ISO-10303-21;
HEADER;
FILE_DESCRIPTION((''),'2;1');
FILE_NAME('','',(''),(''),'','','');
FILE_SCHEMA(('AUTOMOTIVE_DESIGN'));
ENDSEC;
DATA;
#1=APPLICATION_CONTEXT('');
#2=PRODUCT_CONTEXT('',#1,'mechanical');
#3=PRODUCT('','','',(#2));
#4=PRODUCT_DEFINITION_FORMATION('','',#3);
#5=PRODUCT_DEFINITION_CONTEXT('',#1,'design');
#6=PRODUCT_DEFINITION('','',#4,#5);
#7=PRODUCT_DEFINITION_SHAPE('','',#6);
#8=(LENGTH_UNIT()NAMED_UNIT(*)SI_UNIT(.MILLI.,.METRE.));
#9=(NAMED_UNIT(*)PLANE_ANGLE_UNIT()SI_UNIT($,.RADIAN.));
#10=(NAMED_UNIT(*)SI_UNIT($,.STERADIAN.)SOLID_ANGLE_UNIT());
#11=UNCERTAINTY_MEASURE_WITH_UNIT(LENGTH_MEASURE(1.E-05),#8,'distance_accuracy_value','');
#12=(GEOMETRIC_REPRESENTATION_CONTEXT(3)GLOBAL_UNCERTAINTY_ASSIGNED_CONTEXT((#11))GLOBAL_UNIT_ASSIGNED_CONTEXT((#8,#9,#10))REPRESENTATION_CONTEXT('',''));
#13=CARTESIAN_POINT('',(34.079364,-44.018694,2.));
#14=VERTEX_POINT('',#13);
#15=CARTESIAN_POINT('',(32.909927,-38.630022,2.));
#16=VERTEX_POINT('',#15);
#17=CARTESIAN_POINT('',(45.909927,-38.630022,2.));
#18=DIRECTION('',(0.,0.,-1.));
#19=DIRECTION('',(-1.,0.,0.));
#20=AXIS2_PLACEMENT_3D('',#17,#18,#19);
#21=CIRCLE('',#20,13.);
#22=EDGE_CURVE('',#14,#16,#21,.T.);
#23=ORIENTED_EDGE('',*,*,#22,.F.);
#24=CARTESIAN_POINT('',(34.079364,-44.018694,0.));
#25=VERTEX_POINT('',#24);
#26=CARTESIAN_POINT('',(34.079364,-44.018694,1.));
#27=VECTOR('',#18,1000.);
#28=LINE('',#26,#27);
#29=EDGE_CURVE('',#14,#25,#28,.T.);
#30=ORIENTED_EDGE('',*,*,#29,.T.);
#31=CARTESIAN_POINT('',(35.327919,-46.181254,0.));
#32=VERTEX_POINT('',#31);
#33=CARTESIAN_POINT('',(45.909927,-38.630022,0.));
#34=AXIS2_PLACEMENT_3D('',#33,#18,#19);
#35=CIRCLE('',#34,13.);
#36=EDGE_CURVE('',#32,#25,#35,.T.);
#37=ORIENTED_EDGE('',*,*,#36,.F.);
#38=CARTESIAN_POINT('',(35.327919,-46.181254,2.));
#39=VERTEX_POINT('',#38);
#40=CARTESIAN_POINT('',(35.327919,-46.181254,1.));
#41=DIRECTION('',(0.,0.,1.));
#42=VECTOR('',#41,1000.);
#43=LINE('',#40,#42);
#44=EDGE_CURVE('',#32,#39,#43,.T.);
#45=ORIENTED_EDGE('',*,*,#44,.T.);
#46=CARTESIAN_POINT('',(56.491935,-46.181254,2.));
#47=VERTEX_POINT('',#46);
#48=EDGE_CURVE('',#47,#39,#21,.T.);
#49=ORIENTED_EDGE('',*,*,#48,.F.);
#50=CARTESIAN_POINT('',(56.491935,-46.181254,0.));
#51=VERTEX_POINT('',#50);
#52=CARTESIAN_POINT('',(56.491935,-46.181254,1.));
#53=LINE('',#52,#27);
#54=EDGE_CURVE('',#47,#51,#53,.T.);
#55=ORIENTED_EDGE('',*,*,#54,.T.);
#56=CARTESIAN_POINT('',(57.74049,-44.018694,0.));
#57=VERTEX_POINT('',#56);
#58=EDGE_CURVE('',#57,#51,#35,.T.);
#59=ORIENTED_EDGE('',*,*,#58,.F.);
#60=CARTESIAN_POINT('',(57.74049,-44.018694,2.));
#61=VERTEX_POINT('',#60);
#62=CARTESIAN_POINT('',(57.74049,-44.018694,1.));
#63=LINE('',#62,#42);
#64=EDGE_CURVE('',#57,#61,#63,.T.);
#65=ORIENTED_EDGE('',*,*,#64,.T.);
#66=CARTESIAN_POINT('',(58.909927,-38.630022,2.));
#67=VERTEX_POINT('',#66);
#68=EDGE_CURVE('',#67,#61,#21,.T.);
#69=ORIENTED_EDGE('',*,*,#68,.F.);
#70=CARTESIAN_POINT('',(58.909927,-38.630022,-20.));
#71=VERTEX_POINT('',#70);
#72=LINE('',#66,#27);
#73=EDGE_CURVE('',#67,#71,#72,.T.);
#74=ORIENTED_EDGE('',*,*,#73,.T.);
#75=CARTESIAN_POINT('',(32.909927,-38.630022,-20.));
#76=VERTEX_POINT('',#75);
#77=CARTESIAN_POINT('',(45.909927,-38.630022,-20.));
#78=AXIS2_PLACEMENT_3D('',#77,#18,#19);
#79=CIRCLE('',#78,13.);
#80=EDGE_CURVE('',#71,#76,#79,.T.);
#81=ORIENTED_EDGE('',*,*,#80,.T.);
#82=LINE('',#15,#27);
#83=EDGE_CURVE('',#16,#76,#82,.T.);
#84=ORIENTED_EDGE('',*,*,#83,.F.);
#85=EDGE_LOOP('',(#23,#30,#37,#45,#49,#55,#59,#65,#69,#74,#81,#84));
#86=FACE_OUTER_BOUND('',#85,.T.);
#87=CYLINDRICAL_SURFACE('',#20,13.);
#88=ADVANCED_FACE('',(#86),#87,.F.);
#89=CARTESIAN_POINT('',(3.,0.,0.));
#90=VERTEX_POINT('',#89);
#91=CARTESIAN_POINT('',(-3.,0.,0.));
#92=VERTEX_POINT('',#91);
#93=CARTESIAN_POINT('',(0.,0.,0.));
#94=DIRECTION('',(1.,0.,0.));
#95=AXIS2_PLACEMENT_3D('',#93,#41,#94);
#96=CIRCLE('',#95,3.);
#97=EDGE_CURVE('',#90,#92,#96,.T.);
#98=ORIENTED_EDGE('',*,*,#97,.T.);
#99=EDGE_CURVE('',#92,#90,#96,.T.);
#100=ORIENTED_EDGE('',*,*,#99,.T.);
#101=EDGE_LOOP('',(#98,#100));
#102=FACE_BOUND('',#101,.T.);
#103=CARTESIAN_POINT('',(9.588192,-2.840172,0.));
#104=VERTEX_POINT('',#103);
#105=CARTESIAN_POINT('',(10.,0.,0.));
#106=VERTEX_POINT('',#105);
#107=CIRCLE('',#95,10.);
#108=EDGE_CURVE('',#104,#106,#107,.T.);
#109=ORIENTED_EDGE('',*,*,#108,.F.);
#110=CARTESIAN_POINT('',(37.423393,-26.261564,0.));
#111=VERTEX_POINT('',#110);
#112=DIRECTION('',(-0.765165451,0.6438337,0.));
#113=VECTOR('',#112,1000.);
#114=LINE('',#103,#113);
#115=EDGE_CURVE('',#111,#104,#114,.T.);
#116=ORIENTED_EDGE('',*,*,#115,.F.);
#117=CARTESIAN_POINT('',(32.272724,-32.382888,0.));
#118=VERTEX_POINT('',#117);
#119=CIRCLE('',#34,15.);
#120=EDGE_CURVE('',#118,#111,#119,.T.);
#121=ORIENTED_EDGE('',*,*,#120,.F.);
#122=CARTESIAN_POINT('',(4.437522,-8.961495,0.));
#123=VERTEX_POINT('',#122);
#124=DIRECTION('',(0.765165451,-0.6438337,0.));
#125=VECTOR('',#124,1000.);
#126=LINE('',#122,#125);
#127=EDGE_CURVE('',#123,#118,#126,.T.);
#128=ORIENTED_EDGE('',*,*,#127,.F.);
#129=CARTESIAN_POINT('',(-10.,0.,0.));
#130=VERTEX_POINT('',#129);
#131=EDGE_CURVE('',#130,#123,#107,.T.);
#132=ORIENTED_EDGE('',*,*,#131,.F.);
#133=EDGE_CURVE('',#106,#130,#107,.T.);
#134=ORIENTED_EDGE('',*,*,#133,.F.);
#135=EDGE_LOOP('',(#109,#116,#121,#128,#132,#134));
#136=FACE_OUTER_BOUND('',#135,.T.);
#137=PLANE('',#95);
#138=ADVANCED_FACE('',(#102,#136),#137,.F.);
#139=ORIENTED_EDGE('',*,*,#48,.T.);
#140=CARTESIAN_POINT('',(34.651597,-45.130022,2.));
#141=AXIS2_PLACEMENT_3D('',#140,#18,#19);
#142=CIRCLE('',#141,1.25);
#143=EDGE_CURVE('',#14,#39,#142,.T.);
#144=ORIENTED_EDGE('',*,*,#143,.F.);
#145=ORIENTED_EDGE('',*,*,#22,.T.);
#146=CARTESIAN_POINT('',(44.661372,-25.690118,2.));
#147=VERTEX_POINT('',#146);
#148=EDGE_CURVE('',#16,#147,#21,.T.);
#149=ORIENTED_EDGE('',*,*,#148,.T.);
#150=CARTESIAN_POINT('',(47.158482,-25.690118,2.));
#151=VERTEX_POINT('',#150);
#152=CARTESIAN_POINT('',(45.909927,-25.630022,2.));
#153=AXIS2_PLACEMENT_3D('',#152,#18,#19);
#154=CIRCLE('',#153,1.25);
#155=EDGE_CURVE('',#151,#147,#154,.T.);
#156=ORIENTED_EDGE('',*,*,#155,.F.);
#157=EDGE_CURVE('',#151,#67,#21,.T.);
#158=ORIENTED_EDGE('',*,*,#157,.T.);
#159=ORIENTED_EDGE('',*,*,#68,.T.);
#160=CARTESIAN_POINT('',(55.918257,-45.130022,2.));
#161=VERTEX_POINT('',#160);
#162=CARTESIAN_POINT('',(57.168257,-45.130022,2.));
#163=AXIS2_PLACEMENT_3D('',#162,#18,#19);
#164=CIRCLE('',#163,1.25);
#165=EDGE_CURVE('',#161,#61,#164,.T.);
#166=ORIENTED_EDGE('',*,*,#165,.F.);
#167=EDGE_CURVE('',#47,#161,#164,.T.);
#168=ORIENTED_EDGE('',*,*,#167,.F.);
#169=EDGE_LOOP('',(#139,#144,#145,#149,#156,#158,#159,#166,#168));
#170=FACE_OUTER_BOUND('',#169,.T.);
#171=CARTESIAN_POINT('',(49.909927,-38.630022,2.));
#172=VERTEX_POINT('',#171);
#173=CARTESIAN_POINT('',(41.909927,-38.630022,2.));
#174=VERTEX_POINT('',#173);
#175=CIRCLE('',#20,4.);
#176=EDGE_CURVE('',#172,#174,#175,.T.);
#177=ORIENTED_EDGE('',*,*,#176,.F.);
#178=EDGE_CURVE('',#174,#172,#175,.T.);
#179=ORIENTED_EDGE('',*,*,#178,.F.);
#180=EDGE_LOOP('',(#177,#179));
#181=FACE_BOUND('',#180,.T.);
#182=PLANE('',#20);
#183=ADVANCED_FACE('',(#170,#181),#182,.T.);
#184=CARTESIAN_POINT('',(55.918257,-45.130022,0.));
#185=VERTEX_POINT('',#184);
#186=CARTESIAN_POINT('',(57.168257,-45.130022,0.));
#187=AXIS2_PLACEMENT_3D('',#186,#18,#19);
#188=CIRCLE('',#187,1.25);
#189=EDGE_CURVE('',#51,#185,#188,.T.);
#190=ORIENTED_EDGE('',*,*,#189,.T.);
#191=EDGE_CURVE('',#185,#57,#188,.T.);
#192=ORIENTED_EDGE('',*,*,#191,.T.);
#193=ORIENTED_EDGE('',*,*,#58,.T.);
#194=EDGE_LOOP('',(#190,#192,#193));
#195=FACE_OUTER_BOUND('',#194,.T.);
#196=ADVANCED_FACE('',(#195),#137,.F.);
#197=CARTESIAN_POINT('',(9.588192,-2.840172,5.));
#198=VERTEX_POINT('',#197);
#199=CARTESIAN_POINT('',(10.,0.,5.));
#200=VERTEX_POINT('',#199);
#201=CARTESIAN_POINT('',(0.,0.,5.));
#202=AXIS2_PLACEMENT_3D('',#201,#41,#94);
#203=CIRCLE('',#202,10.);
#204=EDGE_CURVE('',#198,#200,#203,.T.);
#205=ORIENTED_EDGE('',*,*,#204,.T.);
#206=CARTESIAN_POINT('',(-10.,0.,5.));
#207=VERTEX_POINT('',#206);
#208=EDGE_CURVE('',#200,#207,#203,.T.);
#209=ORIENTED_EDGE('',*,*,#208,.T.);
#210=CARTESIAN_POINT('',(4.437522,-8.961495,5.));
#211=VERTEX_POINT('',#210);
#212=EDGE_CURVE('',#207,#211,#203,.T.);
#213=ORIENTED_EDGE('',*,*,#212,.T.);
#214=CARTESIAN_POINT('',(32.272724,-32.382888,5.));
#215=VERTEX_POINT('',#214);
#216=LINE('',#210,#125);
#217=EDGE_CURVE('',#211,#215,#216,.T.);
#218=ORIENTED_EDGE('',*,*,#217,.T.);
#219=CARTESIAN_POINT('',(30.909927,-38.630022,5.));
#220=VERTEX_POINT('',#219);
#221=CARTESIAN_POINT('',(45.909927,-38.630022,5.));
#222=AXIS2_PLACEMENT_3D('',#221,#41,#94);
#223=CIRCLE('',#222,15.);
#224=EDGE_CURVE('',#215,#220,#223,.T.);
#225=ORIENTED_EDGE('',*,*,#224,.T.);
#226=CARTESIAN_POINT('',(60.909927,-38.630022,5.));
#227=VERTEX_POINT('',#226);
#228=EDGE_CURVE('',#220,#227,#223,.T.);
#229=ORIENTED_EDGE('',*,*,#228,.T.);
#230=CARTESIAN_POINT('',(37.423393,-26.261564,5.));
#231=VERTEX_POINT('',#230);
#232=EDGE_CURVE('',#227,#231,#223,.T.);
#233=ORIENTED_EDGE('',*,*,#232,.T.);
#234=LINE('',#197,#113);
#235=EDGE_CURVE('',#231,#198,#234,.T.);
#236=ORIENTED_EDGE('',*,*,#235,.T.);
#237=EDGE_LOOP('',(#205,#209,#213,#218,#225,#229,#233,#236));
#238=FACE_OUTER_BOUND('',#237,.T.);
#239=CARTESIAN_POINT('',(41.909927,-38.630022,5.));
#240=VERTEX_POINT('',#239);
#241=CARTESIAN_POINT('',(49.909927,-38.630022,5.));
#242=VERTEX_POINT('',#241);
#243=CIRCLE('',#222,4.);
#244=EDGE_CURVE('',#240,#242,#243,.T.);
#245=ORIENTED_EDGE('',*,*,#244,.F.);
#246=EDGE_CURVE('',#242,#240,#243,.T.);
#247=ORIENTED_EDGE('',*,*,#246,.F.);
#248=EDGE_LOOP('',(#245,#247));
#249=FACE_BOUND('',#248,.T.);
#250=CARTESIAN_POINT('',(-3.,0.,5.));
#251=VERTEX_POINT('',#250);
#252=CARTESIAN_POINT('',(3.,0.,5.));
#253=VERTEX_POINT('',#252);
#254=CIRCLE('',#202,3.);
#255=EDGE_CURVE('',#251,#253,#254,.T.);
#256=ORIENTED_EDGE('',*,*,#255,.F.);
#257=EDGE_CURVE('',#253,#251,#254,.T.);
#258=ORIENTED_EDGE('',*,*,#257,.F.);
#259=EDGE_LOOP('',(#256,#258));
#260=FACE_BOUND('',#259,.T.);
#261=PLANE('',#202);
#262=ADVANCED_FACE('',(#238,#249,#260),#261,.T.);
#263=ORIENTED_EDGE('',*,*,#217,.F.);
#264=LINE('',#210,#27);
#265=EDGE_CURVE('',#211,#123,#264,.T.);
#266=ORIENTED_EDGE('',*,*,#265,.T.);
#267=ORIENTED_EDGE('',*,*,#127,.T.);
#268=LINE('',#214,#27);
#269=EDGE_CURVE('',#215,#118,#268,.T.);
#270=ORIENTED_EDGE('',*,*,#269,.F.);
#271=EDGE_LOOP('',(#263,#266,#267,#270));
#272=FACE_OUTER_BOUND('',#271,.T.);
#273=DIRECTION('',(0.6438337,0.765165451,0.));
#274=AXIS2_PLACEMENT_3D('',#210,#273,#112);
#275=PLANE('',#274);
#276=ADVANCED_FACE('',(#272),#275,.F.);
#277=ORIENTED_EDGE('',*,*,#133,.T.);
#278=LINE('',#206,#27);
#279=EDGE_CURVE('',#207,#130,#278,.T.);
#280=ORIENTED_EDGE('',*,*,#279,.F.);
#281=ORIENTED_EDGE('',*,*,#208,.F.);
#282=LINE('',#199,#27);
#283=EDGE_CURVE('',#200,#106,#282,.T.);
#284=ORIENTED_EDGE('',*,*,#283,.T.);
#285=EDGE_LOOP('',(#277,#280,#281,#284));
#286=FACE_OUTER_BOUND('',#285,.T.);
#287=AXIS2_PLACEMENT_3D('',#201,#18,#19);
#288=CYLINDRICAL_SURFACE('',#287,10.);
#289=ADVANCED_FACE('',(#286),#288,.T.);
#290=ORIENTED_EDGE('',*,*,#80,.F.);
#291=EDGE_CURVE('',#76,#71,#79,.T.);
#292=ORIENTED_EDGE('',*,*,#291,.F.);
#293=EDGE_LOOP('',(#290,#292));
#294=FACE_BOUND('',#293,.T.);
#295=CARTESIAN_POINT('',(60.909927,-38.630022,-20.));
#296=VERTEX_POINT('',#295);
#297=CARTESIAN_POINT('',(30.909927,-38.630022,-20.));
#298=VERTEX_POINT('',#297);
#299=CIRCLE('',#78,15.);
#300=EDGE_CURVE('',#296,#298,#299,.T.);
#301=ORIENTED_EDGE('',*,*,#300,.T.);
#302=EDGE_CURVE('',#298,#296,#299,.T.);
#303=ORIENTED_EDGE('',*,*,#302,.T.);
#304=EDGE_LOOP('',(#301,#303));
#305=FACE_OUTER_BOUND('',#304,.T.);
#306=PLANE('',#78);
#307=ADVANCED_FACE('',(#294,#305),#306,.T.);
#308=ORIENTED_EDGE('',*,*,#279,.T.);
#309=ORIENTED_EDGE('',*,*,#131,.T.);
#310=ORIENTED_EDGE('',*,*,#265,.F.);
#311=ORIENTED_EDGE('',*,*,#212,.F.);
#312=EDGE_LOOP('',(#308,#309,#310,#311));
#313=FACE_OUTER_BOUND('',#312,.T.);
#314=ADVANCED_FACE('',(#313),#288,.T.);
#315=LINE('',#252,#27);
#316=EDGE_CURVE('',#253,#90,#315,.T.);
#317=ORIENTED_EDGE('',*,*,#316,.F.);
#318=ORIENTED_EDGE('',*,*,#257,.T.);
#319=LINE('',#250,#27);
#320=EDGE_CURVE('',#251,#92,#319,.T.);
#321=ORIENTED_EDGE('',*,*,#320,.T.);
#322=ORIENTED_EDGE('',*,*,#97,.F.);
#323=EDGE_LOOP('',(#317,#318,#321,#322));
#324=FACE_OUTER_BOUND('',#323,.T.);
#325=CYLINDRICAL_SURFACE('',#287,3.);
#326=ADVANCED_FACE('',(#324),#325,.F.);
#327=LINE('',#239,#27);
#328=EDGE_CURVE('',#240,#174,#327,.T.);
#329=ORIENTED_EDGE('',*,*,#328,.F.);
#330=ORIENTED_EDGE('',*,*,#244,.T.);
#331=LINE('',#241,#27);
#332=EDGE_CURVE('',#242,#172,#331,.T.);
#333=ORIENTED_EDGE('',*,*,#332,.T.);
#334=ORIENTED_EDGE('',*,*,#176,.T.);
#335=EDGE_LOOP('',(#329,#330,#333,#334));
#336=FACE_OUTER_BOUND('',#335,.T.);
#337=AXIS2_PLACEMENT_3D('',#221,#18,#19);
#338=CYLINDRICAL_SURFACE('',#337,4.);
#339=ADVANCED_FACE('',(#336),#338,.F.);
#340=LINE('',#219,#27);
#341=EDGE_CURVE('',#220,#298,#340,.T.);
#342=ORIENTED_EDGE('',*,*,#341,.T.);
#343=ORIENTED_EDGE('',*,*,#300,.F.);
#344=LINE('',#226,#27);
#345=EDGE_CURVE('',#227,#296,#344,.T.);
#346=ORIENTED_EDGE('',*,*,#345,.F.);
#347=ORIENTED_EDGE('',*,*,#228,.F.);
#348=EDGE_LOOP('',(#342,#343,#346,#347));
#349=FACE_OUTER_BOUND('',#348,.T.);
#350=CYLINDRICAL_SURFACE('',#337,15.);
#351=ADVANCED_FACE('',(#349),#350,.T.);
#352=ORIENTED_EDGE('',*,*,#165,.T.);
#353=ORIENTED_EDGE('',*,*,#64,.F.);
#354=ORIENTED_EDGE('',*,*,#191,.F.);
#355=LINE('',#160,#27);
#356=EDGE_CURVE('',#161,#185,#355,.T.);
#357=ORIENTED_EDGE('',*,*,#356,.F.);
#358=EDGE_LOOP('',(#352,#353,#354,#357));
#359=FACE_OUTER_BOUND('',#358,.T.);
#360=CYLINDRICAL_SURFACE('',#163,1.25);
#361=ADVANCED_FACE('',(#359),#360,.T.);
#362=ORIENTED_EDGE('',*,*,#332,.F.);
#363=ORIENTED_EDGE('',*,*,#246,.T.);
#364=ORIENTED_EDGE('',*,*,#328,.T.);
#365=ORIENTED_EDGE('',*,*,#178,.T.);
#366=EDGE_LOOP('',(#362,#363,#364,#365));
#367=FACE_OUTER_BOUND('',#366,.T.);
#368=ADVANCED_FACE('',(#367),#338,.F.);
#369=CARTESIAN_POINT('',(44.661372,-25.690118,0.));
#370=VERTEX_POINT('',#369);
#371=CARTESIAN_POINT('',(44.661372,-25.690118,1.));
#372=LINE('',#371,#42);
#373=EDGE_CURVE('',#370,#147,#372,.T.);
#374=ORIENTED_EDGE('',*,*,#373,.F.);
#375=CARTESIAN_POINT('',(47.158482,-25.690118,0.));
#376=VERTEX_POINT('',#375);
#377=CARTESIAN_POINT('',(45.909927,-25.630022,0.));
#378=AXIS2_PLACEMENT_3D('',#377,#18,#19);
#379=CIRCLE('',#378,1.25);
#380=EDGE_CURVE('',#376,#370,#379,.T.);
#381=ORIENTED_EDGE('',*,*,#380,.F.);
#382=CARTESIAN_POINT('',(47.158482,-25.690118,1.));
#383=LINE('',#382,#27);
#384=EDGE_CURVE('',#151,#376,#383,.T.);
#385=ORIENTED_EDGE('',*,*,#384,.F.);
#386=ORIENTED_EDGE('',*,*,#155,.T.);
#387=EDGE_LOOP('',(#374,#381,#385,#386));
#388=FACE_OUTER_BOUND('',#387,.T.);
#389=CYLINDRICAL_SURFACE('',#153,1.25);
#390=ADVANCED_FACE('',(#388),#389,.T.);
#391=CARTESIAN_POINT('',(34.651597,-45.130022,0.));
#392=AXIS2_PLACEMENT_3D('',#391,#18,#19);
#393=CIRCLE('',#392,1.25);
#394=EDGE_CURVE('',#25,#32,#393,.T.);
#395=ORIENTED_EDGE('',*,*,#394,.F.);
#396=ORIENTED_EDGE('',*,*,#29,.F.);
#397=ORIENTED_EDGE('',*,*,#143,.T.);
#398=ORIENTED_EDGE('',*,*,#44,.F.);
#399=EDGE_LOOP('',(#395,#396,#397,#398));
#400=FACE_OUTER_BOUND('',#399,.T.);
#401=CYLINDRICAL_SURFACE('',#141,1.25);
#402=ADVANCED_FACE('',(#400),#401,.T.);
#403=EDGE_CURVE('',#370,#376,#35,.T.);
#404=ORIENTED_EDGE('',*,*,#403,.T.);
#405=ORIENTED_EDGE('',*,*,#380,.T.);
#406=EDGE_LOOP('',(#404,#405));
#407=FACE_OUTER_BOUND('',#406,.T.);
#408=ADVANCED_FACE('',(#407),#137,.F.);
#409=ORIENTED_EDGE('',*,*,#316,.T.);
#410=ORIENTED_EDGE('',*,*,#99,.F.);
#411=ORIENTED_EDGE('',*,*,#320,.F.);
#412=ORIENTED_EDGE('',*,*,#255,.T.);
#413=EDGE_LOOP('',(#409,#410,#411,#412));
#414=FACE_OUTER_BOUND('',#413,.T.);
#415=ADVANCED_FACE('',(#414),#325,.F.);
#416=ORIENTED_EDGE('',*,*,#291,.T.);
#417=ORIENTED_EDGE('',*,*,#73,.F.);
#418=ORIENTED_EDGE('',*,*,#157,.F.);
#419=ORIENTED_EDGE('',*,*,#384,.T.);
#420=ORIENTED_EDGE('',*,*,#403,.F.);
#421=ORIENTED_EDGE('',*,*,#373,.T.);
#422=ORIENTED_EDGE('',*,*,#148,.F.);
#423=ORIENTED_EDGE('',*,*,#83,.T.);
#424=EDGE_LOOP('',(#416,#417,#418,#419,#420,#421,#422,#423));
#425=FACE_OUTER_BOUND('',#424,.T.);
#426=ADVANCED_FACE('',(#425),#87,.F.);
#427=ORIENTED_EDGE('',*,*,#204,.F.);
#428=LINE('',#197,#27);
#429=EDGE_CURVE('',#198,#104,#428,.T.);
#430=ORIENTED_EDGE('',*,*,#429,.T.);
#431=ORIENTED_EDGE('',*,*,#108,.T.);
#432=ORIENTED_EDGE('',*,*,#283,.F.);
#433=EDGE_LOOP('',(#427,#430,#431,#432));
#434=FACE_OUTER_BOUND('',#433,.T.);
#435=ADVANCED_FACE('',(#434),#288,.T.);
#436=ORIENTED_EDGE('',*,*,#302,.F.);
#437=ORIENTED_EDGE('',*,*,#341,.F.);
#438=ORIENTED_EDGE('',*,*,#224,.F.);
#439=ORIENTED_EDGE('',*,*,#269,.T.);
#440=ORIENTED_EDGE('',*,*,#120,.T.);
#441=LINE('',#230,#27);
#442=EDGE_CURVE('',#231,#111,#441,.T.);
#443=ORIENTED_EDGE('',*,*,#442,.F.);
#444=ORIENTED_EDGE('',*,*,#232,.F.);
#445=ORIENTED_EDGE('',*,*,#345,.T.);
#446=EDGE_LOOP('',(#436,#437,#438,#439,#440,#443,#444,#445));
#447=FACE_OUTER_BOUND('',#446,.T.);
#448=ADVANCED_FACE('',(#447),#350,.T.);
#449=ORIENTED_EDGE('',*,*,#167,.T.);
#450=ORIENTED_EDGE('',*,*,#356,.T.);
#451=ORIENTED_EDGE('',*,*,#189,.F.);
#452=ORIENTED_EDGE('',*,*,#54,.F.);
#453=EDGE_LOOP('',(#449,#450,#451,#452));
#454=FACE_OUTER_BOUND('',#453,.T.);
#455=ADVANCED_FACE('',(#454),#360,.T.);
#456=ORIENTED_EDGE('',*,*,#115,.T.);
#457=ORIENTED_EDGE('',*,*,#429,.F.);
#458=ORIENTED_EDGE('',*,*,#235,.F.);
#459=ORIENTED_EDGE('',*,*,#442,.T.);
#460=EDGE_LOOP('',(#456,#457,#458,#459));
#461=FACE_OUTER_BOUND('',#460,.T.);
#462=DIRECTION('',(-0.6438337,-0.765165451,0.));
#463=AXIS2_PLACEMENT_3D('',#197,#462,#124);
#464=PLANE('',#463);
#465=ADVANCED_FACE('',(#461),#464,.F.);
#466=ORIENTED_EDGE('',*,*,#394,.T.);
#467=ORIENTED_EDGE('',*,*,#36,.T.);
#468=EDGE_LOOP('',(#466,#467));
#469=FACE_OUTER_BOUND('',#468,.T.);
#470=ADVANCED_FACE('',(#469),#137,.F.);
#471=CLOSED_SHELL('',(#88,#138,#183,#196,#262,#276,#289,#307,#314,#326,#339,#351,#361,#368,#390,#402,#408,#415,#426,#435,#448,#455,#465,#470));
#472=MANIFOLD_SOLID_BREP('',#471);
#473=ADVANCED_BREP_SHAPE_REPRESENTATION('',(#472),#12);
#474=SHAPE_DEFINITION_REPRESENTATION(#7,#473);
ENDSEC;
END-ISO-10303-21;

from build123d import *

# Parameters (mm, degrees)
SKETCH1_R           = 3
SKETCH1_R_2         = 4
BOSS_EXTRUDE1_DEPTH = 5
SKETCH2_R           = 13
CUT_EXTRUDE1_DEPTH  = 2
SKETCH4_R           = 1.25
BOSS_EXTRUDE2_DEPTH = 2
BOSS_EXTRUDE3_START = 20
SKETCH5_R           = 15
SKETCH5_R_2         = 13
BOSS_EXTRUDE3_DEPTH = 20


with BuildPart() as part:
    # Sketch1 → Boss-Extrude1 (new body)
    with BuildSketch(Plane.XY):
        with BuildLine():
            Line((4.437522393, -8.961495132), (32.27272364, -32.382887973))
            ThreePointArc((32.27272364, -32.382887973), (57.387408796, -48.287527496), (37.423393239, -26.261564368))
            Line((37.423393239, -26.261564368), (9.588191993, -2.840171527))
            ThreePointArc((9.588191993, -2.840171527), (-7.651654506, 6.438336999), (4.437522393, -8.961495132))
        make_face()
        Circle(SKETCH1_R, mode=Mode.SUBTRACT)
        with Locations((45.909927037, -38.630021997)):
            Circle(SKETCH1_R_2, mode=Mode.SUBTRACT)
    extrude(amount=BOSS_EXTRUDE1_DEPTH)

    # Sketch2 → Cut-Extrude1 (cut)
    with BuildSketch(Plane(origin=(0, 0, 0), x_dir=(-1, 0, 0), z_dir=(0, 0, -1))):
        with Locations((-45.909927037, -38.630021997)):
            Circle(SKETCH2_R)
    extrude(amount=-CUT_EXTRUDE1_DEPTH, mode=Mode.SUBTRACT)

    # Sketch4 → Boss-Extrude2 (add)
    with BuildSketch(Plane(origin=(0, 0, 0), x_dir=(-1, 0, 0), z_dir=(0, 0, -1))):
        with Locations((-45.909927037, -25.630021997)):
            Circle(SKETCH4_R)
        with Locations((-57.168257286, -45.130021997)):
            Circle(SKETCH4_R)
        with Locations((-34.651596788, -45.130021997)):
            Circle(SKETCH4_R)
    extrude(amount=-BOSS_EXTRUDE2_DEPTH)

    # Sketch5 → Boss-Extrude3 (add)
    with BuildSketch(Plane(origin=(0, 0, 0), x_dir=(-1, 0, 0), z_dir=(0, 0, -1)).offset(BOSS_EXTRUDE3_START)):
        with Locations((-45.909927037, -38.630021997)):
            Circle(SKETCH5_R)
        with Locations((-45.909927037, -38.630021997)):
            Circle(SKETCH5_R_2, mode=Mode.SUBTRACT)
    extrude(amount=-BOSS_EXTRUDE3_DEPTH)


solid = part.part
